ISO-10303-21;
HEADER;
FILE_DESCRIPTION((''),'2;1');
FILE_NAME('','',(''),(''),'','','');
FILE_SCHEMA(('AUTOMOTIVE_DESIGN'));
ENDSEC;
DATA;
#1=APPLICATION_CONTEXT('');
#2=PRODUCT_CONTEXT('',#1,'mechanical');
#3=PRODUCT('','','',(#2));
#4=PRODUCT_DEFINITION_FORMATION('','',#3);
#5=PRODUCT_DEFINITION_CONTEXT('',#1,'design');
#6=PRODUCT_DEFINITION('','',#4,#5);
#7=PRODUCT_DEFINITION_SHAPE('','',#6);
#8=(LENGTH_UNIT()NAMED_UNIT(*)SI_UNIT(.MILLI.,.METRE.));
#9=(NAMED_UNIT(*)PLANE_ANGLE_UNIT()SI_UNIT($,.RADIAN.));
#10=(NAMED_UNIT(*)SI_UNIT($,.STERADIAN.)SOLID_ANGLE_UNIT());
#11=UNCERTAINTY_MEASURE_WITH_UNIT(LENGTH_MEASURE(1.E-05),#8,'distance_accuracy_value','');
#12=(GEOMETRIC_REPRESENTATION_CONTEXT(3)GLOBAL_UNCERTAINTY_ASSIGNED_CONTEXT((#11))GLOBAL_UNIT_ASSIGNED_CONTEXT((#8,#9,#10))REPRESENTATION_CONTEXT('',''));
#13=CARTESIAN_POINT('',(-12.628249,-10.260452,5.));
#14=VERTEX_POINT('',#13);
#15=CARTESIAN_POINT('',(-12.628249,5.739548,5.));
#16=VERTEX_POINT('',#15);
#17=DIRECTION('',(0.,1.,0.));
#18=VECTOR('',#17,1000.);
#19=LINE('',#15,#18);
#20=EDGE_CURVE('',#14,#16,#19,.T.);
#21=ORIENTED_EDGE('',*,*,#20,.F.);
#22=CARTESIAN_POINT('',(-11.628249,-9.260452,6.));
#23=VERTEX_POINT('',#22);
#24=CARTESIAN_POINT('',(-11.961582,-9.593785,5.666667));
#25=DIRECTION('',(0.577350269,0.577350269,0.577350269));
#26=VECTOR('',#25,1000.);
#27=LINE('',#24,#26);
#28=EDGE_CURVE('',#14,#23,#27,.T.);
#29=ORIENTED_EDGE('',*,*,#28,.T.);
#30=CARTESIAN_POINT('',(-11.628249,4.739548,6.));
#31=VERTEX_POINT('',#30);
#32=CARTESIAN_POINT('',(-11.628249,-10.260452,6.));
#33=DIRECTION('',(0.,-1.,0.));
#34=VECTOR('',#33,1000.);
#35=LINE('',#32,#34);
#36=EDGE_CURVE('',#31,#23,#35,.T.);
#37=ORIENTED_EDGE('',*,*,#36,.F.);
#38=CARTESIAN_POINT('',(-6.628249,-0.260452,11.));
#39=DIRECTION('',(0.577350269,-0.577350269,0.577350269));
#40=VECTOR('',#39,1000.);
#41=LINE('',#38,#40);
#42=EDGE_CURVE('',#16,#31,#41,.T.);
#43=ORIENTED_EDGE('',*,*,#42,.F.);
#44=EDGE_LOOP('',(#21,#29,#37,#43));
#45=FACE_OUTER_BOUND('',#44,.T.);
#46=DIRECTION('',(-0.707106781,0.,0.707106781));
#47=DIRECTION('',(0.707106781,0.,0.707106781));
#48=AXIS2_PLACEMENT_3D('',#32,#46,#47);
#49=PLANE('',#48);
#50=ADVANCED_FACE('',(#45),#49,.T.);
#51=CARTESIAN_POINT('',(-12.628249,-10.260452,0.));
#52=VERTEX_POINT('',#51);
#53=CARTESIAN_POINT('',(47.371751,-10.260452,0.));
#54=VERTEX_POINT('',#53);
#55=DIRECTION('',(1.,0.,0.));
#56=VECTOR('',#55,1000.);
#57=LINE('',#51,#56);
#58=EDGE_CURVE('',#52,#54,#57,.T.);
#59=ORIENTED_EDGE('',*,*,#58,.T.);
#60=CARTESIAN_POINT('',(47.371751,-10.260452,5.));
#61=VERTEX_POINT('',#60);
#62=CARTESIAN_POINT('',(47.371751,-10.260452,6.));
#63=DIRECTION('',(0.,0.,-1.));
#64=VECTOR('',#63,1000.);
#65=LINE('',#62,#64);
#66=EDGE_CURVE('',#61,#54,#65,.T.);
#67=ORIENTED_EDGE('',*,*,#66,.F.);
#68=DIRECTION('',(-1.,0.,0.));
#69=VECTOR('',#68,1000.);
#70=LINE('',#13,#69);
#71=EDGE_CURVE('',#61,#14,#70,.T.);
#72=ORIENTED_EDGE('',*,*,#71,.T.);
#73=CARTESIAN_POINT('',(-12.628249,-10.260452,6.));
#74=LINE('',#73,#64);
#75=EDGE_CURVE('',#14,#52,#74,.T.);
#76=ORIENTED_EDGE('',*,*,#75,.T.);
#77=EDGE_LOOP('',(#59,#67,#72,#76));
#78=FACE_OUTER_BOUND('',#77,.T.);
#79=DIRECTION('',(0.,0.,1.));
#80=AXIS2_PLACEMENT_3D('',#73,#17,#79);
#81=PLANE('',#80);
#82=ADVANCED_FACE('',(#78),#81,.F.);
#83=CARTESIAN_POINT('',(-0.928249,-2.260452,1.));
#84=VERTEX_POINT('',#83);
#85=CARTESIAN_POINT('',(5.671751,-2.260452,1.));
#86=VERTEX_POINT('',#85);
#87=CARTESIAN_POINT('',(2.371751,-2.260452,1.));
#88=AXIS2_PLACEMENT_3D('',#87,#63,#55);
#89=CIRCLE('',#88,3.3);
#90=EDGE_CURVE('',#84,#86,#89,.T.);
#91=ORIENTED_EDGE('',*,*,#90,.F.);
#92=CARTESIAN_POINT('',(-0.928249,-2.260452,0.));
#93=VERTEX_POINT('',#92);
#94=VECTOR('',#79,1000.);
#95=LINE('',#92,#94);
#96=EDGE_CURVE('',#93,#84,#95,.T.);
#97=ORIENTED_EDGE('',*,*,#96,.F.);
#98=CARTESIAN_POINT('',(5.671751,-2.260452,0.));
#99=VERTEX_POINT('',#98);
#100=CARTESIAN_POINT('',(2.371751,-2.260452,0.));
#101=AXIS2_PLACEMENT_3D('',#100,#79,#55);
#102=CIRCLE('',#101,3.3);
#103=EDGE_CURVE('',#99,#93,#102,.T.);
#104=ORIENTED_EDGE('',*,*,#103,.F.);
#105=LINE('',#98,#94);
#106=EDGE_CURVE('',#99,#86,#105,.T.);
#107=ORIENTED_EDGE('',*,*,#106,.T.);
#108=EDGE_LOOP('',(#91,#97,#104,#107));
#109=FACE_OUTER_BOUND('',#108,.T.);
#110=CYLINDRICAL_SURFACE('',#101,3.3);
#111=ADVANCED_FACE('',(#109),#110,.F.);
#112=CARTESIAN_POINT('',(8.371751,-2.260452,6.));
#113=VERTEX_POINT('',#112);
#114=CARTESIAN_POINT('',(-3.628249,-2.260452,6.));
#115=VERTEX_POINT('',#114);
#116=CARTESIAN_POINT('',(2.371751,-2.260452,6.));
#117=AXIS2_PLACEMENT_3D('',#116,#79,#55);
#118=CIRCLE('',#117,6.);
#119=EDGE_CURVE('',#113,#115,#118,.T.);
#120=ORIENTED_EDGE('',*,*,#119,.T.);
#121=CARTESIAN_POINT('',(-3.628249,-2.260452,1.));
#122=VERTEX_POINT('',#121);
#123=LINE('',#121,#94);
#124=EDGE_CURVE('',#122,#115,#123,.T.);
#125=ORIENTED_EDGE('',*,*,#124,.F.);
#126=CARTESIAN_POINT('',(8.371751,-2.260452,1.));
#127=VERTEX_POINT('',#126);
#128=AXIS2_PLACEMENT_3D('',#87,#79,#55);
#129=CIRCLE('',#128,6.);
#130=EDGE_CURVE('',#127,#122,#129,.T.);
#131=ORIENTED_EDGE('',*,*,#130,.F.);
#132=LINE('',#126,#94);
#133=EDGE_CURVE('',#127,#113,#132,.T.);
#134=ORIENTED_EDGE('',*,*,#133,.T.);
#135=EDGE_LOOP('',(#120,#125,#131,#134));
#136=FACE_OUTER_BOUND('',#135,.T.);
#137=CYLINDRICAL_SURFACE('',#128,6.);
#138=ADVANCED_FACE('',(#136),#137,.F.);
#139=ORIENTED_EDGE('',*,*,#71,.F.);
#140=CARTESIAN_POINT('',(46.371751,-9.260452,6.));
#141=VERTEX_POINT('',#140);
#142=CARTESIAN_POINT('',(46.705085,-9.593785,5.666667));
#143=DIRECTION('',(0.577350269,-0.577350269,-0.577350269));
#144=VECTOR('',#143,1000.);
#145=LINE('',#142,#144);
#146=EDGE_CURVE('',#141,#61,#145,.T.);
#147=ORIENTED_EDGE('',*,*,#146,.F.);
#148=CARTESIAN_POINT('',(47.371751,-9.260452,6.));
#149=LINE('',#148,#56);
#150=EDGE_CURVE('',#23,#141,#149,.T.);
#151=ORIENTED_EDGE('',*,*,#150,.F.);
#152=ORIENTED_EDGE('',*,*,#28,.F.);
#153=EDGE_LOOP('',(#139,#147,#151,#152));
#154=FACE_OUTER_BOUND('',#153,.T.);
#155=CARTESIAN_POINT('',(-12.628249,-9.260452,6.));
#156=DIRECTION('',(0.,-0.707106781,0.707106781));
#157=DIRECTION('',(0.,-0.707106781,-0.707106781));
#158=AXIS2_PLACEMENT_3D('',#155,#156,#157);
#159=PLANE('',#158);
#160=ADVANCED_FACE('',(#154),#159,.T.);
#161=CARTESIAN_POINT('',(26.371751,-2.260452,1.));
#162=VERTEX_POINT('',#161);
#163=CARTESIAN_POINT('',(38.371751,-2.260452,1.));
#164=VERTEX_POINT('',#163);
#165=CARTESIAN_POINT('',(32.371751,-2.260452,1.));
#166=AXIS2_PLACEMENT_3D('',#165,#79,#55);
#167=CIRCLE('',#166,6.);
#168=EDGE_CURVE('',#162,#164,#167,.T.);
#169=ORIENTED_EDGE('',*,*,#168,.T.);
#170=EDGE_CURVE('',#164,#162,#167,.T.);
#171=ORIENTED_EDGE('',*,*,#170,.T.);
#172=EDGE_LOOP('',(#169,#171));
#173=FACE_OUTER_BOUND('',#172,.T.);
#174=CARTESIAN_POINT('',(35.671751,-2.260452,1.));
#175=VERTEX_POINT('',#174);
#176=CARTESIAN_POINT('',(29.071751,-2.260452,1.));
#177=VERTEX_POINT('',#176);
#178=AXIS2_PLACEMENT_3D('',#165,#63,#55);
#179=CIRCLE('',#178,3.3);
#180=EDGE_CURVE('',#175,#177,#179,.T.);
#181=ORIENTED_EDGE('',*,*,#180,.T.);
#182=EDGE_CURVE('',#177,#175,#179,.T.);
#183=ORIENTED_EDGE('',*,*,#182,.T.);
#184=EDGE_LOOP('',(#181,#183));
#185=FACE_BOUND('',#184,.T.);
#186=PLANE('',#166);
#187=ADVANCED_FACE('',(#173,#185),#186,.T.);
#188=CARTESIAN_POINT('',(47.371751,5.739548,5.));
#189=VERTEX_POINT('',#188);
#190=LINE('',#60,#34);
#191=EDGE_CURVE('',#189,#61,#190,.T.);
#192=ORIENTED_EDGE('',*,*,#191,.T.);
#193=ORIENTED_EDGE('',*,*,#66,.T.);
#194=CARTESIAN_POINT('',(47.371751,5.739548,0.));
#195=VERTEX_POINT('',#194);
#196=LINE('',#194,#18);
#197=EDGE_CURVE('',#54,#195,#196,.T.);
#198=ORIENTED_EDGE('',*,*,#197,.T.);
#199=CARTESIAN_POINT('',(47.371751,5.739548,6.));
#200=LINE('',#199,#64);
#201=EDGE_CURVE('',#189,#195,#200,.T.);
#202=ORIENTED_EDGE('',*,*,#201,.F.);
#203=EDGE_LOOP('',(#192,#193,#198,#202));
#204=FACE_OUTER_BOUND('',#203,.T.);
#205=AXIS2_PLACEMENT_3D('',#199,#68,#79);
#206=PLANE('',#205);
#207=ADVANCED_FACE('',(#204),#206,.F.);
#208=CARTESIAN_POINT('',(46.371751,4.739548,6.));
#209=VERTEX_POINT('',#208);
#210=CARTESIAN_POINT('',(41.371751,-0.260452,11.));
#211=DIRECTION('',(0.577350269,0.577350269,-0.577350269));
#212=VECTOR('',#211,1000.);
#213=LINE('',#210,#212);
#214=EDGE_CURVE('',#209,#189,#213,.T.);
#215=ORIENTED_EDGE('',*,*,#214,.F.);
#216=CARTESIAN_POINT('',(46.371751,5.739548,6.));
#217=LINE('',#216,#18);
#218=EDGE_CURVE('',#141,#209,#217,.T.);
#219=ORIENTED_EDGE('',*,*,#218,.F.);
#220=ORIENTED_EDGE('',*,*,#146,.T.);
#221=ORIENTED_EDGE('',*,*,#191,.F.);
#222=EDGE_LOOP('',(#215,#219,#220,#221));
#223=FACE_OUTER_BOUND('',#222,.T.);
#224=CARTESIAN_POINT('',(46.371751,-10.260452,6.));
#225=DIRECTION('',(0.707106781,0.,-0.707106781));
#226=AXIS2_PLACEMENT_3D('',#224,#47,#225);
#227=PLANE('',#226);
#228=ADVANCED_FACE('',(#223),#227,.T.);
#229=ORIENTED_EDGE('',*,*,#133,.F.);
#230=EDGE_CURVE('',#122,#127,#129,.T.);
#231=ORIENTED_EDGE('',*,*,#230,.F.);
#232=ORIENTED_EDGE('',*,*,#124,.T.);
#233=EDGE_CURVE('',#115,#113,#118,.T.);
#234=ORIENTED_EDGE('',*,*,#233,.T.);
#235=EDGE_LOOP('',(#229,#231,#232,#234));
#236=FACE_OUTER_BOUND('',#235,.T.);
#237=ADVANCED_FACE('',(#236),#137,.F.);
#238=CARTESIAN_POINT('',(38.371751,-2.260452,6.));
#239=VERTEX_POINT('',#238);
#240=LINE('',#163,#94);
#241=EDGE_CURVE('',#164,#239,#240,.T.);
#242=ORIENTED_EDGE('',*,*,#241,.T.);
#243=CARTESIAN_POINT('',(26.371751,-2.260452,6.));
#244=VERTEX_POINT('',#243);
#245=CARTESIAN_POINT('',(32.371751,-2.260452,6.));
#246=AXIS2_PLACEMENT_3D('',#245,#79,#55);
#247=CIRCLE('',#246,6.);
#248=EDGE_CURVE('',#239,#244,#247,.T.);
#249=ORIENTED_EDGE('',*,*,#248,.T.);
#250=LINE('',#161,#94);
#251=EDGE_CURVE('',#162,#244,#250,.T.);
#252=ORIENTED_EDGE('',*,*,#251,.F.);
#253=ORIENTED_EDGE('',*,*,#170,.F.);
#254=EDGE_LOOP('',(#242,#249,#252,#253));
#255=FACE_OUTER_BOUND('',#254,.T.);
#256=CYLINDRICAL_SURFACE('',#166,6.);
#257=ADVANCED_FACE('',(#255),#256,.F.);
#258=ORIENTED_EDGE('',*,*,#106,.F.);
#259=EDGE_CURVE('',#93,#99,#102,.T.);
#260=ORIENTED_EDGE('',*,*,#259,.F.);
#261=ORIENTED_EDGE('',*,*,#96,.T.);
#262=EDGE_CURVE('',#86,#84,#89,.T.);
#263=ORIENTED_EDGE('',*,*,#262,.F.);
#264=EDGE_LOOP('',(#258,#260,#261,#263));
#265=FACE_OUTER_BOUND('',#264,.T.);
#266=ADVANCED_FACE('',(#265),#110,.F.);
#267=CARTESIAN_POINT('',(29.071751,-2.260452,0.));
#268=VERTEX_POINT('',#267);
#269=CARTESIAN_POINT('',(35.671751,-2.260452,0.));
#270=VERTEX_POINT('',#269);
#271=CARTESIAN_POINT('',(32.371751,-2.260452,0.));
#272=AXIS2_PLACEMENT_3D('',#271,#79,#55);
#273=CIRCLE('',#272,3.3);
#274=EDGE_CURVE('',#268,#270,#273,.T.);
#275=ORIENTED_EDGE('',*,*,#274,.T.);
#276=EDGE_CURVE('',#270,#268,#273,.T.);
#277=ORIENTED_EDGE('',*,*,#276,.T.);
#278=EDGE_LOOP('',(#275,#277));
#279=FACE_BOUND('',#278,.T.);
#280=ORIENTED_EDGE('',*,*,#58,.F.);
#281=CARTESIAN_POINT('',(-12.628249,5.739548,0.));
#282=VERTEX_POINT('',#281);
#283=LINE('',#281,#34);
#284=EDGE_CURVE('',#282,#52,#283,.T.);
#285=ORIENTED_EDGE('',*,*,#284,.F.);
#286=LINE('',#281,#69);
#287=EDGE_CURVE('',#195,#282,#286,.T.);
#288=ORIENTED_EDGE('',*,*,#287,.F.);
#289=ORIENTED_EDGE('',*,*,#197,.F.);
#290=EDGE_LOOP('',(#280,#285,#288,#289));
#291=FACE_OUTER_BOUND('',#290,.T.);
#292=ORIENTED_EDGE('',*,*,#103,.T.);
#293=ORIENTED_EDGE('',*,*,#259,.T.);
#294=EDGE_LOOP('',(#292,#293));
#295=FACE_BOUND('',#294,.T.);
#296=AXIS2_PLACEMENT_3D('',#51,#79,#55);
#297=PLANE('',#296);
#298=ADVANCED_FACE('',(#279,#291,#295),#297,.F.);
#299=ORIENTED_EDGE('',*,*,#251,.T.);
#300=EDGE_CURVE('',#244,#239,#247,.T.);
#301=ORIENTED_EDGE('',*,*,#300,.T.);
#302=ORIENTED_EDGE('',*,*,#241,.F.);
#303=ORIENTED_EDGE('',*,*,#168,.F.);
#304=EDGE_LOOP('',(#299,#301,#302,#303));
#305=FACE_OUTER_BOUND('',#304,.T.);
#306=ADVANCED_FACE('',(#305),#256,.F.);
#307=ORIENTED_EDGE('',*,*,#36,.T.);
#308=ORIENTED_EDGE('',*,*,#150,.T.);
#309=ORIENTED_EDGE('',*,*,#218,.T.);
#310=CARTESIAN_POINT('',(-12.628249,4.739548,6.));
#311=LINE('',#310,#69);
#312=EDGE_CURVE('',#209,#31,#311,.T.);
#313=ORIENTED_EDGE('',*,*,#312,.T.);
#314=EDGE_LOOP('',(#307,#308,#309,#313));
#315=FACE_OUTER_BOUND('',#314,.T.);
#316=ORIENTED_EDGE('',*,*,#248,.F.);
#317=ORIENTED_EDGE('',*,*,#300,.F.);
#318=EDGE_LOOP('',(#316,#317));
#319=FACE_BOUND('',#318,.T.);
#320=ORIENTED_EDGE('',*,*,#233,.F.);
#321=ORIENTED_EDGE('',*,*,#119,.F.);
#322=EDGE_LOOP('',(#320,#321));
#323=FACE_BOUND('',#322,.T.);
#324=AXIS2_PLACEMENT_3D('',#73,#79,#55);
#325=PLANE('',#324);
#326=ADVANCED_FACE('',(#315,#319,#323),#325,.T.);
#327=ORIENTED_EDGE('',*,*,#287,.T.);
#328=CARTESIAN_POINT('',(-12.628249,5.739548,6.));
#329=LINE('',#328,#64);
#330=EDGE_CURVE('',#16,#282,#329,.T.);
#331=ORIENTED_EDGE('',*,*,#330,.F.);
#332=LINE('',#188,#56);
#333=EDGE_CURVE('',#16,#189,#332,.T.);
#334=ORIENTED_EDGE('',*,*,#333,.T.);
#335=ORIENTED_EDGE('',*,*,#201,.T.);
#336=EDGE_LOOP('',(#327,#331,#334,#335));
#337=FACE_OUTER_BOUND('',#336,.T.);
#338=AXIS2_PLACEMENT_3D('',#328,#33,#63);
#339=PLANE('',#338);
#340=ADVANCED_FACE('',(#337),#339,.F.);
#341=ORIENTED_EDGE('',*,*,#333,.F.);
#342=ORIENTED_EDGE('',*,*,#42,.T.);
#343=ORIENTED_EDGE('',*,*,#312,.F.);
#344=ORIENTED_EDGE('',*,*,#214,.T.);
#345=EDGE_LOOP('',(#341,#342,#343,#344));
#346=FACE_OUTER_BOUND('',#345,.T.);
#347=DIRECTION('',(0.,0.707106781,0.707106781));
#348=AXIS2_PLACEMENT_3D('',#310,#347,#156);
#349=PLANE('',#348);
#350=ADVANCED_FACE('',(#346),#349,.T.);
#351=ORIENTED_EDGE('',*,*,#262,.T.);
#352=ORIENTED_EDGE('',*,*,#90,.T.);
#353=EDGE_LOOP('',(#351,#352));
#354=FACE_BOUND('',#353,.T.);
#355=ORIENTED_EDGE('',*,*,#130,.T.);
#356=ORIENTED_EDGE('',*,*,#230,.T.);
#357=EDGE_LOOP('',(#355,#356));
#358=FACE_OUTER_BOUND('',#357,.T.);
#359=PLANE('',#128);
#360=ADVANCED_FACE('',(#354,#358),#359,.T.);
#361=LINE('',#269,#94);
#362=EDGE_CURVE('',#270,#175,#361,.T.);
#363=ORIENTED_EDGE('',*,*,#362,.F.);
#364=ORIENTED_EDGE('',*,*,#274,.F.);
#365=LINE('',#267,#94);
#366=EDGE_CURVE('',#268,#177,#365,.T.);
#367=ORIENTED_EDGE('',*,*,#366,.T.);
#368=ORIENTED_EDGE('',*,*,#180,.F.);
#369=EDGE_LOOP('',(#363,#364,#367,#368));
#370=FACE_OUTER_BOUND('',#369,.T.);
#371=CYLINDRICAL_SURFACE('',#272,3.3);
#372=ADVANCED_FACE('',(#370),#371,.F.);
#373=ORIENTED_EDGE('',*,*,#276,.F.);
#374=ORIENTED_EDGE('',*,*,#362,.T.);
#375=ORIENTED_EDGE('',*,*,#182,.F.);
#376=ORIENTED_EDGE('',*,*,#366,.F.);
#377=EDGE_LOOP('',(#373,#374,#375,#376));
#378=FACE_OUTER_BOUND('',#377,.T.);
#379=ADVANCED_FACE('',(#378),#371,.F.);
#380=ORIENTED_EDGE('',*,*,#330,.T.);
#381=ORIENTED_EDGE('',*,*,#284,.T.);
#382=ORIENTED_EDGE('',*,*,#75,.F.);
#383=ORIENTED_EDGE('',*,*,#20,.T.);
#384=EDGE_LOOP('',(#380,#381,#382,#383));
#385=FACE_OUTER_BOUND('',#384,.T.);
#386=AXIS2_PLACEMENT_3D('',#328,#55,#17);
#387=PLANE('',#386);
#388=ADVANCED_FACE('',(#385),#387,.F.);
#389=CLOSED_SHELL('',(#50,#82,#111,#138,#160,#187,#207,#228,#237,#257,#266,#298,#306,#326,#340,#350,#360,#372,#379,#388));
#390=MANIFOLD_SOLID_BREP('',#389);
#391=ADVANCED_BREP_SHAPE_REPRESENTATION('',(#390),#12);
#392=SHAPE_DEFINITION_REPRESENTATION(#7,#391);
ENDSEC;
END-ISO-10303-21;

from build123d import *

# Parameters (mm, degrees)
SKETCH1_W          = 60
SKETCH1_H          = 16
BASE_EXTRUDE_DEPTH = 6
SKETCH2_R          = 3.3
CUT_EXTRUDE1_DEPTH = 49.840144417
SKETCH3_R          = 6
CUT_EXTRUDE2_DEPTH = 5
LPATTERN1_COUNT    = 2
LPATTERN1_PITCH    = 30
CHAMFER1_SIZE      = 1


with BuildPart() as part:
    # Sketch1 → Base-Extrude (new body)
    with BuildSketch(Plane.XY):
        with Locations((17.371751412, -2.260451977)):
            Rectangle(SKETCH1_W, SKETCH1_H)
    extrude(amount=BASE_EXTRUDE_DEPTH)

    # Sketch2 → Cut-Extrude1 (cut, through all)
    with BuildSketch(Plane.XY.offset(6)):
        with Locations((2.371751412, -2.260451977)):
            Circle(SKETCH2_R)
    cut_extrude1 = extrude(amount=-CUT_EXTRUDE1_DEPTH, mode=Mode.SUBTRACT)

    # Sketch3 → Cut-Extrude2 (cut)
    with BuildSketch(Plane.XY.offset(6)):
        with Locations((2.371751412, -2.260451977)):
            Circle(SKETCH3_R)
    cut_extrude2 = extrude(amount=-CUT_EXTRUDE2_DEPTH, mode=Mode.SUBTRACT)

    # LPattern1: Cut-Extrude1, Cut-Extrude2 ×2
    with Locations(*[(i * LPATTERN1_PITCH, 0, 0) for i in range(1, LPATTERN1_COUNT)]):
        add(cut_extrude1, mode=Mode.SUBTRACT)
        add(cut_extrude2, mode=Mode.SUBTRACT)

    # Chamfer1
    chamfer1_edges = [part.edges().sort_by_distance(p)[0] for p in [
        (47.371751412, -2.260451977, 6),
        (17.371751412, 5.739548023, 6),
        (-12.628248588, -2.260451977, 6),
        (17.371751412, -10.260451977, 6),
    ]]
    chamfer(chamfer1_edges, length=CHAMFER1_SIZE)


solid = part.part
